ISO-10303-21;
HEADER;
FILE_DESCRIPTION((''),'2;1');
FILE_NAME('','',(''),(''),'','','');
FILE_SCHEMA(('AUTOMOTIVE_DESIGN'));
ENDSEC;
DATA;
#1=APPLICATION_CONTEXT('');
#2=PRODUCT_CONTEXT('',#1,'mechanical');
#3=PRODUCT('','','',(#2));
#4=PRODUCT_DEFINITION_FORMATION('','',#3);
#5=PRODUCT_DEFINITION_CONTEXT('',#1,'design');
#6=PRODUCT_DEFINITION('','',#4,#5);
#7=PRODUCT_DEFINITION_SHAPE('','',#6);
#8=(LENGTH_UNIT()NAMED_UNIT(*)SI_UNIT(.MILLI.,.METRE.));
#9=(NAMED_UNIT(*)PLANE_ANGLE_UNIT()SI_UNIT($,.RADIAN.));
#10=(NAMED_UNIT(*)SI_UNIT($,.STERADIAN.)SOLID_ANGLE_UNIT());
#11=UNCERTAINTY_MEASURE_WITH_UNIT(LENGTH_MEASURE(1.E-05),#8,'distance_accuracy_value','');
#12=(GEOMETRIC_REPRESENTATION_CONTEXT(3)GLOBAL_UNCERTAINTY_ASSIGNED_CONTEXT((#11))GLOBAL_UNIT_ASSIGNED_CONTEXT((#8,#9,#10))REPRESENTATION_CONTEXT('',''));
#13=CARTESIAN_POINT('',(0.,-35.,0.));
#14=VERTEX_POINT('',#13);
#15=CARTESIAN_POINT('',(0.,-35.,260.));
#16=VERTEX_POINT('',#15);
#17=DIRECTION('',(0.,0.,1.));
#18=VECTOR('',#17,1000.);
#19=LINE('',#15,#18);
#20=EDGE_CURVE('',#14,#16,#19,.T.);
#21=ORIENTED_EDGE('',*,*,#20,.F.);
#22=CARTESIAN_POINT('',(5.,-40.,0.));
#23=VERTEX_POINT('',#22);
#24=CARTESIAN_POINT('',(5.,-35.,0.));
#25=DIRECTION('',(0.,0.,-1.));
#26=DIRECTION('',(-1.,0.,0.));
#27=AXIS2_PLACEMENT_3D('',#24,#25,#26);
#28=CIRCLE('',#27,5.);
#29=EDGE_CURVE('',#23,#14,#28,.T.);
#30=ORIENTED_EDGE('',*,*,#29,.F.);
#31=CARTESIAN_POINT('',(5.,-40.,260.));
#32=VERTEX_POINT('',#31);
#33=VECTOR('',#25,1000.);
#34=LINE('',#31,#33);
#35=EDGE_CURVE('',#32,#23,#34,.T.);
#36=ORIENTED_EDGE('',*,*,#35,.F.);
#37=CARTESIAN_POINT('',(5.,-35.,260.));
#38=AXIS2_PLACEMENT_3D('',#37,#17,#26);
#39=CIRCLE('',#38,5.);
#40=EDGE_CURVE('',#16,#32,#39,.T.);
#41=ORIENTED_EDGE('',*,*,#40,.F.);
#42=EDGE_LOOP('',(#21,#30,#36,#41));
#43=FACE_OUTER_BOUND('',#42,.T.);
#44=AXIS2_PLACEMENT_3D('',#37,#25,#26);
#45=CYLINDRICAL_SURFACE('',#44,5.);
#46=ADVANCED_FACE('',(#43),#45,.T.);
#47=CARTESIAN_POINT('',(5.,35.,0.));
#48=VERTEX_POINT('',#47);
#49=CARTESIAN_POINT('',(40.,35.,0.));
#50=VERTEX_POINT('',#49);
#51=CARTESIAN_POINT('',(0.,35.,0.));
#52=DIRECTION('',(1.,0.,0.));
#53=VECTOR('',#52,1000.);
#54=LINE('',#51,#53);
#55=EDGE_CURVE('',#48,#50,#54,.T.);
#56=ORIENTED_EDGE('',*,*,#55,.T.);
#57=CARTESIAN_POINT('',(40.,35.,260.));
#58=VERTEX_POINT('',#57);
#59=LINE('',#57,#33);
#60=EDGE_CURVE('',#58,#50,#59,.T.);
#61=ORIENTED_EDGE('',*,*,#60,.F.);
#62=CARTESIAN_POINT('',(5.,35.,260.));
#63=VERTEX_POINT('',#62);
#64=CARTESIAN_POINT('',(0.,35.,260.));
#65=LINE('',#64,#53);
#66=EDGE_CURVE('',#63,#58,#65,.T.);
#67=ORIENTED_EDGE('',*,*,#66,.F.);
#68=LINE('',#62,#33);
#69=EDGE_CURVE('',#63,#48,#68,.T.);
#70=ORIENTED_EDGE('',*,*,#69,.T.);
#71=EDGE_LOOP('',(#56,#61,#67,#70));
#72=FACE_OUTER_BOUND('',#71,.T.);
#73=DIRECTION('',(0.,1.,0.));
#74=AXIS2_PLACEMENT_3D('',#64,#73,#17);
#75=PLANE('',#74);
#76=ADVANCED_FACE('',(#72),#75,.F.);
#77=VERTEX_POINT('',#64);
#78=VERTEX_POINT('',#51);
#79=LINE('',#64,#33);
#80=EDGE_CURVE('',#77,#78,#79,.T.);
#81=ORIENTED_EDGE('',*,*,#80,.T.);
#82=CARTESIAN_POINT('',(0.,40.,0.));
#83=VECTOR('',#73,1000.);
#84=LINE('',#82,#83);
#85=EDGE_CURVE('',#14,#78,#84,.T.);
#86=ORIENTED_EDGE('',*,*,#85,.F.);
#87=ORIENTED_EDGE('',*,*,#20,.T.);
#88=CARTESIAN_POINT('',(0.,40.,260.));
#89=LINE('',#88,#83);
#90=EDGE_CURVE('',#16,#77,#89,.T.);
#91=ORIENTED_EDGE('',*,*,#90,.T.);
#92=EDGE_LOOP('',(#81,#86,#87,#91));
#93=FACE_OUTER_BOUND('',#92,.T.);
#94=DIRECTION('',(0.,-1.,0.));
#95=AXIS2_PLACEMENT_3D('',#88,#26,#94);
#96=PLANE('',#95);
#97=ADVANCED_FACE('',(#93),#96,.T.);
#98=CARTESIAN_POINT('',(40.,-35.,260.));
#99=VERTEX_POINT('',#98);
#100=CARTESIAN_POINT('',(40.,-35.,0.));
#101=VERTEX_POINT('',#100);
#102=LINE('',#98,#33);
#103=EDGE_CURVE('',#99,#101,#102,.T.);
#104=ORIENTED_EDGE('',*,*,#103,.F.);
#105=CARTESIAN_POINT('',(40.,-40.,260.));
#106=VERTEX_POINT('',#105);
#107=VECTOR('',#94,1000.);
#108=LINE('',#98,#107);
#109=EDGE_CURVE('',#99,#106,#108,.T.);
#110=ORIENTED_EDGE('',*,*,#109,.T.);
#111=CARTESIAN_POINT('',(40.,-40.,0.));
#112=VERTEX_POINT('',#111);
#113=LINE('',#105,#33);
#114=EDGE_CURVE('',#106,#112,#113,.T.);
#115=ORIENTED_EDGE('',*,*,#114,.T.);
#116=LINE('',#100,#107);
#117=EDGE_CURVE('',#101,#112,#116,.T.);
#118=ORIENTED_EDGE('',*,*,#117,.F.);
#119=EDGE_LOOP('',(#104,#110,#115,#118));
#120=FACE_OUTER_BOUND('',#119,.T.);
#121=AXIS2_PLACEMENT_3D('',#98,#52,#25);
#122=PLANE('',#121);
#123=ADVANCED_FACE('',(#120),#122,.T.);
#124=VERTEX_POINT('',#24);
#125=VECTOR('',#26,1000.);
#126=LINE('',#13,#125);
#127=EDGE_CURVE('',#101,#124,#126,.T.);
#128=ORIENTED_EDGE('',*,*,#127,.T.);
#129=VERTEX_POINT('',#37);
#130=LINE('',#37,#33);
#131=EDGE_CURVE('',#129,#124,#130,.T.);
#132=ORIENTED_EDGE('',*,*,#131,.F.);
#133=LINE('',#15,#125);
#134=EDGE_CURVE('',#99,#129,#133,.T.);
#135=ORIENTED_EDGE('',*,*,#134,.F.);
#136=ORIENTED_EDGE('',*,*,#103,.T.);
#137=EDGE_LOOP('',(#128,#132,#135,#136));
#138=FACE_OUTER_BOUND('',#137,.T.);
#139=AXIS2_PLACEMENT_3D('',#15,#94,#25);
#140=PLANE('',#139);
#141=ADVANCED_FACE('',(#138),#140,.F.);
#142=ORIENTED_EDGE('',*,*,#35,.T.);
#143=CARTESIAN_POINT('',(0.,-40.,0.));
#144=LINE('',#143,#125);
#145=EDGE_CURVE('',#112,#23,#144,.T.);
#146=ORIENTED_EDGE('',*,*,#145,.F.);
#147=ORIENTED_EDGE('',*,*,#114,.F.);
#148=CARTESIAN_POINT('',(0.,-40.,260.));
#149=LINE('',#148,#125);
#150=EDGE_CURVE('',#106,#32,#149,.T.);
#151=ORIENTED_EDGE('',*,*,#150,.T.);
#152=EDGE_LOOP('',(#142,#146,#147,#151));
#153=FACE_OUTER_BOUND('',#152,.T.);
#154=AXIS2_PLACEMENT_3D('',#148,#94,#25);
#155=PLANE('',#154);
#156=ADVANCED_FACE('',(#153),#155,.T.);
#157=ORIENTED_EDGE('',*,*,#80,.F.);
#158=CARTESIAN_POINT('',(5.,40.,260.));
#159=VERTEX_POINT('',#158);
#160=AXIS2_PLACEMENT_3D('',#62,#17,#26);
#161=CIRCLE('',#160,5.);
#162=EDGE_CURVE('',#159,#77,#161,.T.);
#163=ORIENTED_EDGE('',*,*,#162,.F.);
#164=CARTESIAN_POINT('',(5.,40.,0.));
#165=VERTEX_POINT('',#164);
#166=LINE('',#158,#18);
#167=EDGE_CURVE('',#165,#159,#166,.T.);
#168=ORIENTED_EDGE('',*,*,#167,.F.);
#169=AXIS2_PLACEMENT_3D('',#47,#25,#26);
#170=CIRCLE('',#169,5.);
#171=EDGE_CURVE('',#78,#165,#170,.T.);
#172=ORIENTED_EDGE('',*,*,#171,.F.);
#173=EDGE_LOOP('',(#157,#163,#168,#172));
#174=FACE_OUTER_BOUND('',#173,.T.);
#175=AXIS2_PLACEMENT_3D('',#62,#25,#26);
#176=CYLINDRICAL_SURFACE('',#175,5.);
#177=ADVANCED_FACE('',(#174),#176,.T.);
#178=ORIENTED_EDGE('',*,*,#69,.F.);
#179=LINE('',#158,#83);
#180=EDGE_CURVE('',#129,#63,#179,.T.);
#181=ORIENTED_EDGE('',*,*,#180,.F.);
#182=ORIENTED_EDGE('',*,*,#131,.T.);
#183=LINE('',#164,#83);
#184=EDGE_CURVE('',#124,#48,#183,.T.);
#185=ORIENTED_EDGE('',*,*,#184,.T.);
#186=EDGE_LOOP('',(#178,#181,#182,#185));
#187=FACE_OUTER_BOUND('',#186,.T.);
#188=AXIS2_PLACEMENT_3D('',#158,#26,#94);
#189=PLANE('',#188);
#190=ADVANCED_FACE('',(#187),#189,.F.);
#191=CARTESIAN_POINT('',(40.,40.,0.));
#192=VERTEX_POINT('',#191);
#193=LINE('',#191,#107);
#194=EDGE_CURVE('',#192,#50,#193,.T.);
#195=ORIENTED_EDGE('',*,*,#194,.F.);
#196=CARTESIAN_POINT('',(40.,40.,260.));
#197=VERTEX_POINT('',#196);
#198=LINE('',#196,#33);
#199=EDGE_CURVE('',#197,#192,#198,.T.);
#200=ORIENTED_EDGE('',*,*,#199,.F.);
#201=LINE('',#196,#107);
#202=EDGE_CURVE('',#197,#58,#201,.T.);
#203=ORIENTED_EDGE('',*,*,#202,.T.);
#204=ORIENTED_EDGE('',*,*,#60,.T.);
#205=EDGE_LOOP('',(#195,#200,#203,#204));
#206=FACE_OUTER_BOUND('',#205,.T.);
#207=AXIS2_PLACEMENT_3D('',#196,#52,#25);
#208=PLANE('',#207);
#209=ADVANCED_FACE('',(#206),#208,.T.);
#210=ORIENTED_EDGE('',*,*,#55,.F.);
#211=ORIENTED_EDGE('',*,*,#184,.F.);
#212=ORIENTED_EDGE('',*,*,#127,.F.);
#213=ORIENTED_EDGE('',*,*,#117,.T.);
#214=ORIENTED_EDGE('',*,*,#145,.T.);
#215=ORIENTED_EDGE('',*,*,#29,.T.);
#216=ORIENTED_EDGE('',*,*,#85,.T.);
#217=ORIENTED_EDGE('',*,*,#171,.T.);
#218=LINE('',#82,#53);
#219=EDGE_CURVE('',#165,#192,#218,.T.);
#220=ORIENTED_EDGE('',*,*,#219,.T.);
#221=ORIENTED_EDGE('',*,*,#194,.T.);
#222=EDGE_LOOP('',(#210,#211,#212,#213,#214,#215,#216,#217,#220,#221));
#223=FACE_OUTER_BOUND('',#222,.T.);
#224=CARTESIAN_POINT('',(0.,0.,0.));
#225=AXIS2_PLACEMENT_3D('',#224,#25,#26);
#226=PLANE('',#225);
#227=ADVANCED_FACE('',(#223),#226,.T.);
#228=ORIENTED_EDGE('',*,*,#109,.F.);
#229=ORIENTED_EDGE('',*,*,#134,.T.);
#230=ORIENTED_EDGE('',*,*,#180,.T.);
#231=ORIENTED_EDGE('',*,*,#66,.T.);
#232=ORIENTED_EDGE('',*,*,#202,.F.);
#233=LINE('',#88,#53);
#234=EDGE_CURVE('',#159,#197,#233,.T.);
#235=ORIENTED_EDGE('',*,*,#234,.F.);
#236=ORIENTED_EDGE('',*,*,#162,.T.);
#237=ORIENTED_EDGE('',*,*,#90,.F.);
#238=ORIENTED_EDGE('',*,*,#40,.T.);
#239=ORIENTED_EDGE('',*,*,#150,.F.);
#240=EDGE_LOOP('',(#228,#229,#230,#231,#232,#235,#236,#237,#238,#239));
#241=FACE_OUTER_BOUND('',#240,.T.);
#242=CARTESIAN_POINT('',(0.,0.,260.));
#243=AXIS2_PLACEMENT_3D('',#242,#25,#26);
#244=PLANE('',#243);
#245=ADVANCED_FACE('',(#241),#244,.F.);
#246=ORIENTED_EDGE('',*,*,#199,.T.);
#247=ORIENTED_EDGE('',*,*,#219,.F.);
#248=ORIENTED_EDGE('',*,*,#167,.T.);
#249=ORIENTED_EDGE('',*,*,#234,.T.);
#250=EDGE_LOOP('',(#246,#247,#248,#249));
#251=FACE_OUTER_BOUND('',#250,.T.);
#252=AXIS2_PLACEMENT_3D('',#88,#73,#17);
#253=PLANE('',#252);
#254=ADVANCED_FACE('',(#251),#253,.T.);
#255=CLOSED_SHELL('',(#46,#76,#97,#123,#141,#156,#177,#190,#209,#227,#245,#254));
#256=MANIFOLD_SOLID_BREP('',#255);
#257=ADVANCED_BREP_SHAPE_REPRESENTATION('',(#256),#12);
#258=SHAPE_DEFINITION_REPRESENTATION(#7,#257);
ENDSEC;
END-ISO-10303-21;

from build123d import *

# Parameters (mm, degrees)
EXTRUDE_1_DEPTH = 260
FILLET_1_R      = 5


with BuildPart() as part:
    # 草图1 → 拉伸-薄壁1 (new body)
    with BuildSketch(Plane.XY):
        Polygon((40, 40), (0, 40), (0, -40), (40, -40), (40, -35), (5, -35), (5, 35), (40, 35), align=None)
    extrude(amount=EXTRUDE_1_DEPTH)

    # 圆角1
    fillet_1_edges = [part.edges().sort_by_distance(p)[0] for p in [
        (0, -40, 130),
        (0, 40, 130),
    ]]
    fillet(fillet_1_edges, radius=FILLET_1_R)


solid = part.part
